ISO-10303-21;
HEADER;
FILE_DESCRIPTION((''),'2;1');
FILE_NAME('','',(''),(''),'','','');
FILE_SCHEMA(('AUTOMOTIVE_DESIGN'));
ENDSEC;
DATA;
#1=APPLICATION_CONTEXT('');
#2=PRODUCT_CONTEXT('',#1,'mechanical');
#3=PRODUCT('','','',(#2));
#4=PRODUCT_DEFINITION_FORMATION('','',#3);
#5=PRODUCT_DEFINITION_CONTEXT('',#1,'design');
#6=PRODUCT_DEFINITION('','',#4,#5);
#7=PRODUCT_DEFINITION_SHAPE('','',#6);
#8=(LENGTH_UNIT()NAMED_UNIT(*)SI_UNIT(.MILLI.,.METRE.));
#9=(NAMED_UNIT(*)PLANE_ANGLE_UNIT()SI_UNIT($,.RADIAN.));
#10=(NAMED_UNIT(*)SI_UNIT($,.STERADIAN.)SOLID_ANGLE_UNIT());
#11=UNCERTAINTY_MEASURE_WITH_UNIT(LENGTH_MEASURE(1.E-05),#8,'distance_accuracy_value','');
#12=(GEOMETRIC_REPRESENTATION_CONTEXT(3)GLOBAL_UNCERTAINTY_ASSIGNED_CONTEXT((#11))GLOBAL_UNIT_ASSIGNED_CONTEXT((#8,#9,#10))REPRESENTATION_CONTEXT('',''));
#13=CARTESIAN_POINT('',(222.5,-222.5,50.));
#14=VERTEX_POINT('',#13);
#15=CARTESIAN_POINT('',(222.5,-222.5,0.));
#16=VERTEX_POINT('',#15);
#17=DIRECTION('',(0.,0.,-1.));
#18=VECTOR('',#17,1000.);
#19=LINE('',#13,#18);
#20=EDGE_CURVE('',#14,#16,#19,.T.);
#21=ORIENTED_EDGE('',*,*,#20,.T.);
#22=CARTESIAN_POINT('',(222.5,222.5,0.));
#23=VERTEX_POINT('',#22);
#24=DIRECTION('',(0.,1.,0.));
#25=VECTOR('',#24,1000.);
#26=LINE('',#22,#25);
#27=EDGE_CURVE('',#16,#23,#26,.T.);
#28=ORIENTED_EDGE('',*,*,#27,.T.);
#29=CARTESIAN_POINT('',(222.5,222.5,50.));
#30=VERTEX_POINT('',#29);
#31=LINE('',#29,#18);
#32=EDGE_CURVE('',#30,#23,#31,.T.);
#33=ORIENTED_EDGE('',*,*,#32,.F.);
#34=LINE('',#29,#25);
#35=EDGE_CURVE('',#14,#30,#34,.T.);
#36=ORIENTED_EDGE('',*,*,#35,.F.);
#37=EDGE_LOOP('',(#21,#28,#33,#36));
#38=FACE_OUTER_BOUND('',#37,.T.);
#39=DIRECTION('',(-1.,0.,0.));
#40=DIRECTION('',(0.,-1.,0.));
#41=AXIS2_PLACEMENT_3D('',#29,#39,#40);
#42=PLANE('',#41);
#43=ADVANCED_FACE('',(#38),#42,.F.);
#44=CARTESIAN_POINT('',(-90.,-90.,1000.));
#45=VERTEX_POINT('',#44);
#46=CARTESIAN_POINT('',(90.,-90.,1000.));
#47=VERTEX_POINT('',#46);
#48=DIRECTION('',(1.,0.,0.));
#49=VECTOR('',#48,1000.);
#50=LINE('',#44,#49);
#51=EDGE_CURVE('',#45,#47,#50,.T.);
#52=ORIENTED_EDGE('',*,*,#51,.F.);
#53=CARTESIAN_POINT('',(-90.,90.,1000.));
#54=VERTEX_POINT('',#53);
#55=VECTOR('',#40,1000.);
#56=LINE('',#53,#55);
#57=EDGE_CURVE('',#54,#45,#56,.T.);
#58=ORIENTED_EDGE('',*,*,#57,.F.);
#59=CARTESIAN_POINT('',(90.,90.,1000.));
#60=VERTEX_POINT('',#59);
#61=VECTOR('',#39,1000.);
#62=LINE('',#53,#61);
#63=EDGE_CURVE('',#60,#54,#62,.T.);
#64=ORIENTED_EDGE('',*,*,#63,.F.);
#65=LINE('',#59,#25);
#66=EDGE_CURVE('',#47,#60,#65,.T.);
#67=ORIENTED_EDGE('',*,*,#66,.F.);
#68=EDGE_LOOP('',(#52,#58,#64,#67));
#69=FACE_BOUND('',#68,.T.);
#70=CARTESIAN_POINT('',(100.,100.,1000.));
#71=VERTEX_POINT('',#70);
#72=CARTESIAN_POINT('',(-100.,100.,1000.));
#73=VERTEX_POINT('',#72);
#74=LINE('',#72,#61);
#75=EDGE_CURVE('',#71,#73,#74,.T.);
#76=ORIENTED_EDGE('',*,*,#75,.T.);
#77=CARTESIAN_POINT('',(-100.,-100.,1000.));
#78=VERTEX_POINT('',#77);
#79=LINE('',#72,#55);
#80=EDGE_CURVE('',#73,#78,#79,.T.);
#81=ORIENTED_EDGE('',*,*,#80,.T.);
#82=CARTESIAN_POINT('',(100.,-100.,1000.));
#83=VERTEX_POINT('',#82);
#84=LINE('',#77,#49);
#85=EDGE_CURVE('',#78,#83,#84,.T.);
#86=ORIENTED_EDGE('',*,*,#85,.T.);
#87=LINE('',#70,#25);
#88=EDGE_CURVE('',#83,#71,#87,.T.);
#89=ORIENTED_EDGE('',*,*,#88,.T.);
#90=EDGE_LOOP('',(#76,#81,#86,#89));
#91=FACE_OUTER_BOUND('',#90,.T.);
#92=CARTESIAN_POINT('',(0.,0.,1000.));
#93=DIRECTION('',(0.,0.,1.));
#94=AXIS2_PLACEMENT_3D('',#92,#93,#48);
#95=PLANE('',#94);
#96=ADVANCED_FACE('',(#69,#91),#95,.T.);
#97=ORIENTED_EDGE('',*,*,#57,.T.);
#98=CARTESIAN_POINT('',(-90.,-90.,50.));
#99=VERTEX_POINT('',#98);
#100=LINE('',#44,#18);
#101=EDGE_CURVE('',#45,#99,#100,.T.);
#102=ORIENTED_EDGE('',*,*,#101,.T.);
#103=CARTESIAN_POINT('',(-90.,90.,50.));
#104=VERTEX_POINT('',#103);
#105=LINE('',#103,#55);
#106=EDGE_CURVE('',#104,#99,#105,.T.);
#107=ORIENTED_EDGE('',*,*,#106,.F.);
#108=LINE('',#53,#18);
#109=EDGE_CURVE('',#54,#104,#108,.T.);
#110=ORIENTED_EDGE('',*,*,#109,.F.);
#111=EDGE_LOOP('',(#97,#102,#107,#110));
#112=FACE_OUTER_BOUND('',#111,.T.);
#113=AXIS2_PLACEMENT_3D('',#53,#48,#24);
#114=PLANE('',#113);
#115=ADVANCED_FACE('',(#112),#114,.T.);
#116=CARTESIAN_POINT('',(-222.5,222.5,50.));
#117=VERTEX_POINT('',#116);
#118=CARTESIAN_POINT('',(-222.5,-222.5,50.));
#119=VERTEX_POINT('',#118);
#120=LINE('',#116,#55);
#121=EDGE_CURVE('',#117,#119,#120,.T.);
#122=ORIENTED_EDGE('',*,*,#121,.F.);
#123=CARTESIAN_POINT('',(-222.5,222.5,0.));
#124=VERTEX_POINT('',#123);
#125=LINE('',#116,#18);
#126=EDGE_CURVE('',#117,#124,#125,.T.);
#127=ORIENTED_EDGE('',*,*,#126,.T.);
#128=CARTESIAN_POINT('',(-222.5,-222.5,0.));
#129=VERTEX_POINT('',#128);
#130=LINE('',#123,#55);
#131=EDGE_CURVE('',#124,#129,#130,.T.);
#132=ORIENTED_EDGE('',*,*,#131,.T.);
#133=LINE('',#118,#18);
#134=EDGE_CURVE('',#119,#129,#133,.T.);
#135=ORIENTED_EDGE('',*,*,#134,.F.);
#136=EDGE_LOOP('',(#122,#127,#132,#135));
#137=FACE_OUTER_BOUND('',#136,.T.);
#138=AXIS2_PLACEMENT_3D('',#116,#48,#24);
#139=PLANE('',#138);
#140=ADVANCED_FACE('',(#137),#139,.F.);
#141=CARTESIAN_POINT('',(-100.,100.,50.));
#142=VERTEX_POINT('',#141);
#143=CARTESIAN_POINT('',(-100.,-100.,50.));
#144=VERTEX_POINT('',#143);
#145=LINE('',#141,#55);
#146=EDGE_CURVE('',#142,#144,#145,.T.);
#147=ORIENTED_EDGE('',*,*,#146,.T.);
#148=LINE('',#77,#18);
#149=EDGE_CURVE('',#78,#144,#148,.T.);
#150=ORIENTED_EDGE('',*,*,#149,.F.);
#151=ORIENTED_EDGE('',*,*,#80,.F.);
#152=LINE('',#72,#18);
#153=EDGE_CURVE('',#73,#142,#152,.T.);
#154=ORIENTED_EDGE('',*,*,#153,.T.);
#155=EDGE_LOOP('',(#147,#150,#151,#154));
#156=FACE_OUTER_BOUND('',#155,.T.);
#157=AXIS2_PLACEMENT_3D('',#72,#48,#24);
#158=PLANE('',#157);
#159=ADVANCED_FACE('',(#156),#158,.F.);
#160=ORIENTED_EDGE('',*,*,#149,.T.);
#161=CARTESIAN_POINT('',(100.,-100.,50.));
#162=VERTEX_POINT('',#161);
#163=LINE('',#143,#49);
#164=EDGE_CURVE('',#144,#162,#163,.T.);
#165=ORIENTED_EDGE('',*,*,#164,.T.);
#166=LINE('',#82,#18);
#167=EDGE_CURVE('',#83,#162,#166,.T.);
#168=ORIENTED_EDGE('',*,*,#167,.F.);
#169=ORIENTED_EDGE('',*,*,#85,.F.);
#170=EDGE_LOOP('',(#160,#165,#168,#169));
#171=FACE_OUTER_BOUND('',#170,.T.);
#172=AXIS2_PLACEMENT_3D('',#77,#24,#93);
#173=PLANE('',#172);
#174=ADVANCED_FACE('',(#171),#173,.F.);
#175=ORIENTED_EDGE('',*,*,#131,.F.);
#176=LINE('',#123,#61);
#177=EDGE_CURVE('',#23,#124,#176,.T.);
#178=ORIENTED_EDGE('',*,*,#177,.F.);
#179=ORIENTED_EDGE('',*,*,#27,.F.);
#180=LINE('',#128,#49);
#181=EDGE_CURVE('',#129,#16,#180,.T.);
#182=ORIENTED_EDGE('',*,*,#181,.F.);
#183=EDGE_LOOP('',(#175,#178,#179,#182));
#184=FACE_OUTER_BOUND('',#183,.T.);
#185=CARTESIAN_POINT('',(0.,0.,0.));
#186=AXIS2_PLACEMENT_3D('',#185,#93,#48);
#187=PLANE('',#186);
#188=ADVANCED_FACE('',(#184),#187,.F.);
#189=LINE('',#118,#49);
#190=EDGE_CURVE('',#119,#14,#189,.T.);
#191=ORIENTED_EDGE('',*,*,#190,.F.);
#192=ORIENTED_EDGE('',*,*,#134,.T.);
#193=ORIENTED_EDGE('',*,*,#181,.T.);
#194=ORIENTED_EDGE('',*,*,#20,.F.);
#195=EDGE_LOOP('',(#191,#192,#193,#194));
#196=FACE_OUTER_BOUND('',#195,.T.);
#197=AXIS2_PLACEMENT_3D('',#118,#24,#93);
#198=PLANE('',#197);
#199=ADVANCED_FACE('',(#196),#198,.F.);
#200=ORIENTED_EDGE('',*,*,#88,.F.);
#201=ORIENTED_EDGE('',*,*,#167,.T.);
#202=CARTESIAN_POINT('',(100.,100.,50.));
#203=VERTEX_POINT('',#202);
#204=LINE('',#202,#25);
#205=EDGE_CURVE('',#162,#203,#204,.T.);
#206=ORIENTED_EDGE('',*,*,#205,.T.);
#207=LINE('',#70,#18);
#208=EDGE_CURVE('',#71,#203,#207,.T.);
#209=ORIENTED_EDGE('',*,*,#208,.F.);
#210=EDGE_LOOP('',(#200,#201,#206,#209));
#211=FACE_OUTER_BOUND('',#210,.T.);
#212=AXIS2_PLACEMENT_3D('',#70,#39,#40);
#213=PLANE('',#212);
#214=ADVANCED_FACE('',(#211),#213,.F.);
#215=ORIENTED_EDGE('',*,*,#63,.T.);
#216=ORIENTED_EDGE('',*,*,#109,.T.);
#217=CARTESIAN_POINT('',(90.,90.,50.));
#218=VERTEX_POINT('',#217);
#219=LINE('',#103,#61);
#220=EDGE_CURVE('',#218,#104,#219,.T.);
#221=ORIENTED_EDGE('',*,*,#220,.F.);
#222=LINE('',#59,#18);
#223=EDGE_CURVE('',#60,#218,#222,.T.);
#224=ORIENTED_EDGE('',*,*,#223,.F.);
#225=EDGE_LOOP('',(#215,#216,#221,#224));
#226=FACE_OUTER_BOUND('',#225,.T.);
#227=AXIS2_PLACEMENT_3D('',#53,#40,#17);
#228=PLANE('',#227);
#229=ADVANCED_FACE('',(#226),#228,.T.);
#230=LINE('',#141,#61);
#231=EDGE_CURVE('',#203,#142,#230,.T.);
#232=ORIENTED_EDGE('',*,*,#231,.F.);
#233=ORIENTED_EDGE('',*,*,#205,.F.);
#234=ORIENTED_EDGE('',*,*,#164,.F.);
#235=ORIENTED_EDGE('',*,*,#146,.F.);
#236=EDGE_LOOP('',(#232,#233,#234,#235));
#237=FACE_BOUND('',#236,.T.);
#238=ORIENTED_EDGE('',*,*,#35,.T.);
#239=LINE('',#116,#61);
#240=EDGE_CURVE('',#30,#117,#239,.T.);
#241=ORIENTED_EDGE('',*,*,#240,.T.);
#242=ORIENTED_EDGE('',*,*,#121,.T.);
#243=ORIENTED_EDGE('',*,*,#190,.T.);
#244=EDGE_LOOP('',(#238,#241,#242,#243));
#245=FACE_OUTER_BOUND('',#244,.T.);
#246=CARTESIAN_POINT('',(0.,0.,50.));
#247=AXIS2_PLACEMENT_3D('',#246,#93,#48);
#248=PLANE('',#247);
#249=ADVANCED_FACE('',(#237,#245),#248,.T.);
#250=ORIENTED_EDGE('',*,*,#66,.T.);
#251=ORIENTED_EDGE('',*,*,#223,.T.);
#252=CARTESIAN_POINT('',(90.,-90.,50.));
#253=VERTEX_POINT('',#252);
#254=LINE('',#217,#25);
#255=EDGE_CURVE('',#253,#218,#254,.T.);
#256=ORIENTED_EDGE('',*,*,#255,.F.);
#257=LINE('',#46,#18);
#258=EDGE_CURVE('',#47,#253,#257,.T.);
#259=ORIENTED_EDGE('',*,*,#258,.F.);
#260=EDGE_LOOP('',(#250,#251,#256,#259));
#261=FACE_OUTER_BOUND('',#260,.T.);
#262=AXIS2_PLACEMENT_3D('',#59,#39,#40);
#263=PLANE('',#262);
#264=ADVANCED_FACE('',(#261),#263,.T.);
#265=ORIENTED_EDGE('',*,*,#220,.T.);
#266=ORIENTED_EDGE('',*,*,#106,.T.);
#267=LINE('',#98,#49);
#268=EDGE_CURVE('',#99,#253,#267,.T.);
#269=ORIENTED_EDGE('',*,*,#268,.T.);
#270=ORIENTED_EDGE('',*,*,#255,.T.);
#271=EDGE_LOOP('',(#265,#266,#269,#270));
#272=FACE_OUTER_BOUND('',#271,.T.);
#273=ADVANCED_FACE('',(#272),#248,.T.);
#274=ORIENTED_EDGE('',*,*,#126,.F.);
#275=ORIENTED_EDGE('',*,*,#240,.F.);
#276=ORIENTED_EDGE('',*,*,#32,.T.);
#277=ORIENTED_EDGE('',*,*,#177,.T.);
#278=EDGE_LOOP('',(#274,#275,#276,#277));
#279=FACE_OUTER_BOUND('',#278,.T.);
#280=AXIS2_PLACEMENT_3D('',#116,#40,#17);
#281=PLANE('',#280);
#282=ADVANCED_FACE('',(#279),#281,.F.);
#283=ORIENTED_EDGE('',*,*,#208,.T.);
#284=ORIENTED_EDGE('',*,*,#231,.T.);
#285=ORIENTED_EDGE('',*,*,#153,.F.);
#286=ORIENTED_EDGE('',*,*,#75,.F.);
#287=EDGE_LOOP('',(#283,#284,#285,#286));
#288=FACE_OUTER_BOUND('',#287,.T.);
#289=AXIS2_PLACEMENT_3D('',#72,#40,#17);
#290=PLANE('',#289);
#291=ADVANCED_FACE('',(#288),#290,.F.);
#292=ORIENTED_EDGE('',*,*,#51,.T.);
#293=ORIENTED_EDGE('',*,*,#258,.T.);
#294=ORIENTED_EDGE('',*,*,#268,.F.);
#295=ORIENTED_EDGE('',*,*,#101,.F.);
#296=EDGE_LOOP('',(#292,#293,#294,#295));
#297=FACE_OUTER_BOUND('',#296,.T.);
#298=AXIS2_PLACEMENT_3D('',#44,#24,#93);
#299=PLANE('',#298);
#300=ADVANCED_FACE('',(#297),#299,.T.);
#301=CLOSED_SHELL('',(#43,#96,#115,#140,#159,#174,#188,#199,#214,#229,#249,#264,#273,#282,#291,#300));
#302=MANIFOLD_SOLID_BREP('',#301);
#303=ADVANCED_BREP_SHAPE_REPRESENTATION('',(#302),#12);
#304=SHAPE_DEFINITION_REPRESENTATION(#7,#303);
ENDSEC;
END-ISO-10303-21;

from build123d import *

# Parameters (mm, degrees)
SKETCH1_W           = 445
SKETCH1_H           = 445
BOSS_EXTRUDE1_DEPTH = 50
SKETCH2_W           = 200
SKETCH2_H           = 200
SKETCH2_W_2         = 180
SKETCH2_H_2         = 180
BOSS_EXTRUDE2_DEPTH = 950


with BuildPart() as part:
    # Sketch1 → Boss-Extrude1 (new body)
    with BuildSketch(Plane.XY):
        Rectangle(SKETCH1_W, SKETCH1_H)
    extrude(amount=BOSS_EXTRUDE1_DEPTH)

    # Sketch2 → Boss-Extrude2 (add)
    with BuildSketch(Plane.XY.offset(50)):
        Rectangle(SKETCH2_W, SKETCH2_H)
        Rectangle(SKETCH2_W_2, SKETCH2_H_2, mode=Mode.SUBTRACT)
    extrude(amount=BOSS_EXTRUDE2_DEPTH)


solid = part.part
